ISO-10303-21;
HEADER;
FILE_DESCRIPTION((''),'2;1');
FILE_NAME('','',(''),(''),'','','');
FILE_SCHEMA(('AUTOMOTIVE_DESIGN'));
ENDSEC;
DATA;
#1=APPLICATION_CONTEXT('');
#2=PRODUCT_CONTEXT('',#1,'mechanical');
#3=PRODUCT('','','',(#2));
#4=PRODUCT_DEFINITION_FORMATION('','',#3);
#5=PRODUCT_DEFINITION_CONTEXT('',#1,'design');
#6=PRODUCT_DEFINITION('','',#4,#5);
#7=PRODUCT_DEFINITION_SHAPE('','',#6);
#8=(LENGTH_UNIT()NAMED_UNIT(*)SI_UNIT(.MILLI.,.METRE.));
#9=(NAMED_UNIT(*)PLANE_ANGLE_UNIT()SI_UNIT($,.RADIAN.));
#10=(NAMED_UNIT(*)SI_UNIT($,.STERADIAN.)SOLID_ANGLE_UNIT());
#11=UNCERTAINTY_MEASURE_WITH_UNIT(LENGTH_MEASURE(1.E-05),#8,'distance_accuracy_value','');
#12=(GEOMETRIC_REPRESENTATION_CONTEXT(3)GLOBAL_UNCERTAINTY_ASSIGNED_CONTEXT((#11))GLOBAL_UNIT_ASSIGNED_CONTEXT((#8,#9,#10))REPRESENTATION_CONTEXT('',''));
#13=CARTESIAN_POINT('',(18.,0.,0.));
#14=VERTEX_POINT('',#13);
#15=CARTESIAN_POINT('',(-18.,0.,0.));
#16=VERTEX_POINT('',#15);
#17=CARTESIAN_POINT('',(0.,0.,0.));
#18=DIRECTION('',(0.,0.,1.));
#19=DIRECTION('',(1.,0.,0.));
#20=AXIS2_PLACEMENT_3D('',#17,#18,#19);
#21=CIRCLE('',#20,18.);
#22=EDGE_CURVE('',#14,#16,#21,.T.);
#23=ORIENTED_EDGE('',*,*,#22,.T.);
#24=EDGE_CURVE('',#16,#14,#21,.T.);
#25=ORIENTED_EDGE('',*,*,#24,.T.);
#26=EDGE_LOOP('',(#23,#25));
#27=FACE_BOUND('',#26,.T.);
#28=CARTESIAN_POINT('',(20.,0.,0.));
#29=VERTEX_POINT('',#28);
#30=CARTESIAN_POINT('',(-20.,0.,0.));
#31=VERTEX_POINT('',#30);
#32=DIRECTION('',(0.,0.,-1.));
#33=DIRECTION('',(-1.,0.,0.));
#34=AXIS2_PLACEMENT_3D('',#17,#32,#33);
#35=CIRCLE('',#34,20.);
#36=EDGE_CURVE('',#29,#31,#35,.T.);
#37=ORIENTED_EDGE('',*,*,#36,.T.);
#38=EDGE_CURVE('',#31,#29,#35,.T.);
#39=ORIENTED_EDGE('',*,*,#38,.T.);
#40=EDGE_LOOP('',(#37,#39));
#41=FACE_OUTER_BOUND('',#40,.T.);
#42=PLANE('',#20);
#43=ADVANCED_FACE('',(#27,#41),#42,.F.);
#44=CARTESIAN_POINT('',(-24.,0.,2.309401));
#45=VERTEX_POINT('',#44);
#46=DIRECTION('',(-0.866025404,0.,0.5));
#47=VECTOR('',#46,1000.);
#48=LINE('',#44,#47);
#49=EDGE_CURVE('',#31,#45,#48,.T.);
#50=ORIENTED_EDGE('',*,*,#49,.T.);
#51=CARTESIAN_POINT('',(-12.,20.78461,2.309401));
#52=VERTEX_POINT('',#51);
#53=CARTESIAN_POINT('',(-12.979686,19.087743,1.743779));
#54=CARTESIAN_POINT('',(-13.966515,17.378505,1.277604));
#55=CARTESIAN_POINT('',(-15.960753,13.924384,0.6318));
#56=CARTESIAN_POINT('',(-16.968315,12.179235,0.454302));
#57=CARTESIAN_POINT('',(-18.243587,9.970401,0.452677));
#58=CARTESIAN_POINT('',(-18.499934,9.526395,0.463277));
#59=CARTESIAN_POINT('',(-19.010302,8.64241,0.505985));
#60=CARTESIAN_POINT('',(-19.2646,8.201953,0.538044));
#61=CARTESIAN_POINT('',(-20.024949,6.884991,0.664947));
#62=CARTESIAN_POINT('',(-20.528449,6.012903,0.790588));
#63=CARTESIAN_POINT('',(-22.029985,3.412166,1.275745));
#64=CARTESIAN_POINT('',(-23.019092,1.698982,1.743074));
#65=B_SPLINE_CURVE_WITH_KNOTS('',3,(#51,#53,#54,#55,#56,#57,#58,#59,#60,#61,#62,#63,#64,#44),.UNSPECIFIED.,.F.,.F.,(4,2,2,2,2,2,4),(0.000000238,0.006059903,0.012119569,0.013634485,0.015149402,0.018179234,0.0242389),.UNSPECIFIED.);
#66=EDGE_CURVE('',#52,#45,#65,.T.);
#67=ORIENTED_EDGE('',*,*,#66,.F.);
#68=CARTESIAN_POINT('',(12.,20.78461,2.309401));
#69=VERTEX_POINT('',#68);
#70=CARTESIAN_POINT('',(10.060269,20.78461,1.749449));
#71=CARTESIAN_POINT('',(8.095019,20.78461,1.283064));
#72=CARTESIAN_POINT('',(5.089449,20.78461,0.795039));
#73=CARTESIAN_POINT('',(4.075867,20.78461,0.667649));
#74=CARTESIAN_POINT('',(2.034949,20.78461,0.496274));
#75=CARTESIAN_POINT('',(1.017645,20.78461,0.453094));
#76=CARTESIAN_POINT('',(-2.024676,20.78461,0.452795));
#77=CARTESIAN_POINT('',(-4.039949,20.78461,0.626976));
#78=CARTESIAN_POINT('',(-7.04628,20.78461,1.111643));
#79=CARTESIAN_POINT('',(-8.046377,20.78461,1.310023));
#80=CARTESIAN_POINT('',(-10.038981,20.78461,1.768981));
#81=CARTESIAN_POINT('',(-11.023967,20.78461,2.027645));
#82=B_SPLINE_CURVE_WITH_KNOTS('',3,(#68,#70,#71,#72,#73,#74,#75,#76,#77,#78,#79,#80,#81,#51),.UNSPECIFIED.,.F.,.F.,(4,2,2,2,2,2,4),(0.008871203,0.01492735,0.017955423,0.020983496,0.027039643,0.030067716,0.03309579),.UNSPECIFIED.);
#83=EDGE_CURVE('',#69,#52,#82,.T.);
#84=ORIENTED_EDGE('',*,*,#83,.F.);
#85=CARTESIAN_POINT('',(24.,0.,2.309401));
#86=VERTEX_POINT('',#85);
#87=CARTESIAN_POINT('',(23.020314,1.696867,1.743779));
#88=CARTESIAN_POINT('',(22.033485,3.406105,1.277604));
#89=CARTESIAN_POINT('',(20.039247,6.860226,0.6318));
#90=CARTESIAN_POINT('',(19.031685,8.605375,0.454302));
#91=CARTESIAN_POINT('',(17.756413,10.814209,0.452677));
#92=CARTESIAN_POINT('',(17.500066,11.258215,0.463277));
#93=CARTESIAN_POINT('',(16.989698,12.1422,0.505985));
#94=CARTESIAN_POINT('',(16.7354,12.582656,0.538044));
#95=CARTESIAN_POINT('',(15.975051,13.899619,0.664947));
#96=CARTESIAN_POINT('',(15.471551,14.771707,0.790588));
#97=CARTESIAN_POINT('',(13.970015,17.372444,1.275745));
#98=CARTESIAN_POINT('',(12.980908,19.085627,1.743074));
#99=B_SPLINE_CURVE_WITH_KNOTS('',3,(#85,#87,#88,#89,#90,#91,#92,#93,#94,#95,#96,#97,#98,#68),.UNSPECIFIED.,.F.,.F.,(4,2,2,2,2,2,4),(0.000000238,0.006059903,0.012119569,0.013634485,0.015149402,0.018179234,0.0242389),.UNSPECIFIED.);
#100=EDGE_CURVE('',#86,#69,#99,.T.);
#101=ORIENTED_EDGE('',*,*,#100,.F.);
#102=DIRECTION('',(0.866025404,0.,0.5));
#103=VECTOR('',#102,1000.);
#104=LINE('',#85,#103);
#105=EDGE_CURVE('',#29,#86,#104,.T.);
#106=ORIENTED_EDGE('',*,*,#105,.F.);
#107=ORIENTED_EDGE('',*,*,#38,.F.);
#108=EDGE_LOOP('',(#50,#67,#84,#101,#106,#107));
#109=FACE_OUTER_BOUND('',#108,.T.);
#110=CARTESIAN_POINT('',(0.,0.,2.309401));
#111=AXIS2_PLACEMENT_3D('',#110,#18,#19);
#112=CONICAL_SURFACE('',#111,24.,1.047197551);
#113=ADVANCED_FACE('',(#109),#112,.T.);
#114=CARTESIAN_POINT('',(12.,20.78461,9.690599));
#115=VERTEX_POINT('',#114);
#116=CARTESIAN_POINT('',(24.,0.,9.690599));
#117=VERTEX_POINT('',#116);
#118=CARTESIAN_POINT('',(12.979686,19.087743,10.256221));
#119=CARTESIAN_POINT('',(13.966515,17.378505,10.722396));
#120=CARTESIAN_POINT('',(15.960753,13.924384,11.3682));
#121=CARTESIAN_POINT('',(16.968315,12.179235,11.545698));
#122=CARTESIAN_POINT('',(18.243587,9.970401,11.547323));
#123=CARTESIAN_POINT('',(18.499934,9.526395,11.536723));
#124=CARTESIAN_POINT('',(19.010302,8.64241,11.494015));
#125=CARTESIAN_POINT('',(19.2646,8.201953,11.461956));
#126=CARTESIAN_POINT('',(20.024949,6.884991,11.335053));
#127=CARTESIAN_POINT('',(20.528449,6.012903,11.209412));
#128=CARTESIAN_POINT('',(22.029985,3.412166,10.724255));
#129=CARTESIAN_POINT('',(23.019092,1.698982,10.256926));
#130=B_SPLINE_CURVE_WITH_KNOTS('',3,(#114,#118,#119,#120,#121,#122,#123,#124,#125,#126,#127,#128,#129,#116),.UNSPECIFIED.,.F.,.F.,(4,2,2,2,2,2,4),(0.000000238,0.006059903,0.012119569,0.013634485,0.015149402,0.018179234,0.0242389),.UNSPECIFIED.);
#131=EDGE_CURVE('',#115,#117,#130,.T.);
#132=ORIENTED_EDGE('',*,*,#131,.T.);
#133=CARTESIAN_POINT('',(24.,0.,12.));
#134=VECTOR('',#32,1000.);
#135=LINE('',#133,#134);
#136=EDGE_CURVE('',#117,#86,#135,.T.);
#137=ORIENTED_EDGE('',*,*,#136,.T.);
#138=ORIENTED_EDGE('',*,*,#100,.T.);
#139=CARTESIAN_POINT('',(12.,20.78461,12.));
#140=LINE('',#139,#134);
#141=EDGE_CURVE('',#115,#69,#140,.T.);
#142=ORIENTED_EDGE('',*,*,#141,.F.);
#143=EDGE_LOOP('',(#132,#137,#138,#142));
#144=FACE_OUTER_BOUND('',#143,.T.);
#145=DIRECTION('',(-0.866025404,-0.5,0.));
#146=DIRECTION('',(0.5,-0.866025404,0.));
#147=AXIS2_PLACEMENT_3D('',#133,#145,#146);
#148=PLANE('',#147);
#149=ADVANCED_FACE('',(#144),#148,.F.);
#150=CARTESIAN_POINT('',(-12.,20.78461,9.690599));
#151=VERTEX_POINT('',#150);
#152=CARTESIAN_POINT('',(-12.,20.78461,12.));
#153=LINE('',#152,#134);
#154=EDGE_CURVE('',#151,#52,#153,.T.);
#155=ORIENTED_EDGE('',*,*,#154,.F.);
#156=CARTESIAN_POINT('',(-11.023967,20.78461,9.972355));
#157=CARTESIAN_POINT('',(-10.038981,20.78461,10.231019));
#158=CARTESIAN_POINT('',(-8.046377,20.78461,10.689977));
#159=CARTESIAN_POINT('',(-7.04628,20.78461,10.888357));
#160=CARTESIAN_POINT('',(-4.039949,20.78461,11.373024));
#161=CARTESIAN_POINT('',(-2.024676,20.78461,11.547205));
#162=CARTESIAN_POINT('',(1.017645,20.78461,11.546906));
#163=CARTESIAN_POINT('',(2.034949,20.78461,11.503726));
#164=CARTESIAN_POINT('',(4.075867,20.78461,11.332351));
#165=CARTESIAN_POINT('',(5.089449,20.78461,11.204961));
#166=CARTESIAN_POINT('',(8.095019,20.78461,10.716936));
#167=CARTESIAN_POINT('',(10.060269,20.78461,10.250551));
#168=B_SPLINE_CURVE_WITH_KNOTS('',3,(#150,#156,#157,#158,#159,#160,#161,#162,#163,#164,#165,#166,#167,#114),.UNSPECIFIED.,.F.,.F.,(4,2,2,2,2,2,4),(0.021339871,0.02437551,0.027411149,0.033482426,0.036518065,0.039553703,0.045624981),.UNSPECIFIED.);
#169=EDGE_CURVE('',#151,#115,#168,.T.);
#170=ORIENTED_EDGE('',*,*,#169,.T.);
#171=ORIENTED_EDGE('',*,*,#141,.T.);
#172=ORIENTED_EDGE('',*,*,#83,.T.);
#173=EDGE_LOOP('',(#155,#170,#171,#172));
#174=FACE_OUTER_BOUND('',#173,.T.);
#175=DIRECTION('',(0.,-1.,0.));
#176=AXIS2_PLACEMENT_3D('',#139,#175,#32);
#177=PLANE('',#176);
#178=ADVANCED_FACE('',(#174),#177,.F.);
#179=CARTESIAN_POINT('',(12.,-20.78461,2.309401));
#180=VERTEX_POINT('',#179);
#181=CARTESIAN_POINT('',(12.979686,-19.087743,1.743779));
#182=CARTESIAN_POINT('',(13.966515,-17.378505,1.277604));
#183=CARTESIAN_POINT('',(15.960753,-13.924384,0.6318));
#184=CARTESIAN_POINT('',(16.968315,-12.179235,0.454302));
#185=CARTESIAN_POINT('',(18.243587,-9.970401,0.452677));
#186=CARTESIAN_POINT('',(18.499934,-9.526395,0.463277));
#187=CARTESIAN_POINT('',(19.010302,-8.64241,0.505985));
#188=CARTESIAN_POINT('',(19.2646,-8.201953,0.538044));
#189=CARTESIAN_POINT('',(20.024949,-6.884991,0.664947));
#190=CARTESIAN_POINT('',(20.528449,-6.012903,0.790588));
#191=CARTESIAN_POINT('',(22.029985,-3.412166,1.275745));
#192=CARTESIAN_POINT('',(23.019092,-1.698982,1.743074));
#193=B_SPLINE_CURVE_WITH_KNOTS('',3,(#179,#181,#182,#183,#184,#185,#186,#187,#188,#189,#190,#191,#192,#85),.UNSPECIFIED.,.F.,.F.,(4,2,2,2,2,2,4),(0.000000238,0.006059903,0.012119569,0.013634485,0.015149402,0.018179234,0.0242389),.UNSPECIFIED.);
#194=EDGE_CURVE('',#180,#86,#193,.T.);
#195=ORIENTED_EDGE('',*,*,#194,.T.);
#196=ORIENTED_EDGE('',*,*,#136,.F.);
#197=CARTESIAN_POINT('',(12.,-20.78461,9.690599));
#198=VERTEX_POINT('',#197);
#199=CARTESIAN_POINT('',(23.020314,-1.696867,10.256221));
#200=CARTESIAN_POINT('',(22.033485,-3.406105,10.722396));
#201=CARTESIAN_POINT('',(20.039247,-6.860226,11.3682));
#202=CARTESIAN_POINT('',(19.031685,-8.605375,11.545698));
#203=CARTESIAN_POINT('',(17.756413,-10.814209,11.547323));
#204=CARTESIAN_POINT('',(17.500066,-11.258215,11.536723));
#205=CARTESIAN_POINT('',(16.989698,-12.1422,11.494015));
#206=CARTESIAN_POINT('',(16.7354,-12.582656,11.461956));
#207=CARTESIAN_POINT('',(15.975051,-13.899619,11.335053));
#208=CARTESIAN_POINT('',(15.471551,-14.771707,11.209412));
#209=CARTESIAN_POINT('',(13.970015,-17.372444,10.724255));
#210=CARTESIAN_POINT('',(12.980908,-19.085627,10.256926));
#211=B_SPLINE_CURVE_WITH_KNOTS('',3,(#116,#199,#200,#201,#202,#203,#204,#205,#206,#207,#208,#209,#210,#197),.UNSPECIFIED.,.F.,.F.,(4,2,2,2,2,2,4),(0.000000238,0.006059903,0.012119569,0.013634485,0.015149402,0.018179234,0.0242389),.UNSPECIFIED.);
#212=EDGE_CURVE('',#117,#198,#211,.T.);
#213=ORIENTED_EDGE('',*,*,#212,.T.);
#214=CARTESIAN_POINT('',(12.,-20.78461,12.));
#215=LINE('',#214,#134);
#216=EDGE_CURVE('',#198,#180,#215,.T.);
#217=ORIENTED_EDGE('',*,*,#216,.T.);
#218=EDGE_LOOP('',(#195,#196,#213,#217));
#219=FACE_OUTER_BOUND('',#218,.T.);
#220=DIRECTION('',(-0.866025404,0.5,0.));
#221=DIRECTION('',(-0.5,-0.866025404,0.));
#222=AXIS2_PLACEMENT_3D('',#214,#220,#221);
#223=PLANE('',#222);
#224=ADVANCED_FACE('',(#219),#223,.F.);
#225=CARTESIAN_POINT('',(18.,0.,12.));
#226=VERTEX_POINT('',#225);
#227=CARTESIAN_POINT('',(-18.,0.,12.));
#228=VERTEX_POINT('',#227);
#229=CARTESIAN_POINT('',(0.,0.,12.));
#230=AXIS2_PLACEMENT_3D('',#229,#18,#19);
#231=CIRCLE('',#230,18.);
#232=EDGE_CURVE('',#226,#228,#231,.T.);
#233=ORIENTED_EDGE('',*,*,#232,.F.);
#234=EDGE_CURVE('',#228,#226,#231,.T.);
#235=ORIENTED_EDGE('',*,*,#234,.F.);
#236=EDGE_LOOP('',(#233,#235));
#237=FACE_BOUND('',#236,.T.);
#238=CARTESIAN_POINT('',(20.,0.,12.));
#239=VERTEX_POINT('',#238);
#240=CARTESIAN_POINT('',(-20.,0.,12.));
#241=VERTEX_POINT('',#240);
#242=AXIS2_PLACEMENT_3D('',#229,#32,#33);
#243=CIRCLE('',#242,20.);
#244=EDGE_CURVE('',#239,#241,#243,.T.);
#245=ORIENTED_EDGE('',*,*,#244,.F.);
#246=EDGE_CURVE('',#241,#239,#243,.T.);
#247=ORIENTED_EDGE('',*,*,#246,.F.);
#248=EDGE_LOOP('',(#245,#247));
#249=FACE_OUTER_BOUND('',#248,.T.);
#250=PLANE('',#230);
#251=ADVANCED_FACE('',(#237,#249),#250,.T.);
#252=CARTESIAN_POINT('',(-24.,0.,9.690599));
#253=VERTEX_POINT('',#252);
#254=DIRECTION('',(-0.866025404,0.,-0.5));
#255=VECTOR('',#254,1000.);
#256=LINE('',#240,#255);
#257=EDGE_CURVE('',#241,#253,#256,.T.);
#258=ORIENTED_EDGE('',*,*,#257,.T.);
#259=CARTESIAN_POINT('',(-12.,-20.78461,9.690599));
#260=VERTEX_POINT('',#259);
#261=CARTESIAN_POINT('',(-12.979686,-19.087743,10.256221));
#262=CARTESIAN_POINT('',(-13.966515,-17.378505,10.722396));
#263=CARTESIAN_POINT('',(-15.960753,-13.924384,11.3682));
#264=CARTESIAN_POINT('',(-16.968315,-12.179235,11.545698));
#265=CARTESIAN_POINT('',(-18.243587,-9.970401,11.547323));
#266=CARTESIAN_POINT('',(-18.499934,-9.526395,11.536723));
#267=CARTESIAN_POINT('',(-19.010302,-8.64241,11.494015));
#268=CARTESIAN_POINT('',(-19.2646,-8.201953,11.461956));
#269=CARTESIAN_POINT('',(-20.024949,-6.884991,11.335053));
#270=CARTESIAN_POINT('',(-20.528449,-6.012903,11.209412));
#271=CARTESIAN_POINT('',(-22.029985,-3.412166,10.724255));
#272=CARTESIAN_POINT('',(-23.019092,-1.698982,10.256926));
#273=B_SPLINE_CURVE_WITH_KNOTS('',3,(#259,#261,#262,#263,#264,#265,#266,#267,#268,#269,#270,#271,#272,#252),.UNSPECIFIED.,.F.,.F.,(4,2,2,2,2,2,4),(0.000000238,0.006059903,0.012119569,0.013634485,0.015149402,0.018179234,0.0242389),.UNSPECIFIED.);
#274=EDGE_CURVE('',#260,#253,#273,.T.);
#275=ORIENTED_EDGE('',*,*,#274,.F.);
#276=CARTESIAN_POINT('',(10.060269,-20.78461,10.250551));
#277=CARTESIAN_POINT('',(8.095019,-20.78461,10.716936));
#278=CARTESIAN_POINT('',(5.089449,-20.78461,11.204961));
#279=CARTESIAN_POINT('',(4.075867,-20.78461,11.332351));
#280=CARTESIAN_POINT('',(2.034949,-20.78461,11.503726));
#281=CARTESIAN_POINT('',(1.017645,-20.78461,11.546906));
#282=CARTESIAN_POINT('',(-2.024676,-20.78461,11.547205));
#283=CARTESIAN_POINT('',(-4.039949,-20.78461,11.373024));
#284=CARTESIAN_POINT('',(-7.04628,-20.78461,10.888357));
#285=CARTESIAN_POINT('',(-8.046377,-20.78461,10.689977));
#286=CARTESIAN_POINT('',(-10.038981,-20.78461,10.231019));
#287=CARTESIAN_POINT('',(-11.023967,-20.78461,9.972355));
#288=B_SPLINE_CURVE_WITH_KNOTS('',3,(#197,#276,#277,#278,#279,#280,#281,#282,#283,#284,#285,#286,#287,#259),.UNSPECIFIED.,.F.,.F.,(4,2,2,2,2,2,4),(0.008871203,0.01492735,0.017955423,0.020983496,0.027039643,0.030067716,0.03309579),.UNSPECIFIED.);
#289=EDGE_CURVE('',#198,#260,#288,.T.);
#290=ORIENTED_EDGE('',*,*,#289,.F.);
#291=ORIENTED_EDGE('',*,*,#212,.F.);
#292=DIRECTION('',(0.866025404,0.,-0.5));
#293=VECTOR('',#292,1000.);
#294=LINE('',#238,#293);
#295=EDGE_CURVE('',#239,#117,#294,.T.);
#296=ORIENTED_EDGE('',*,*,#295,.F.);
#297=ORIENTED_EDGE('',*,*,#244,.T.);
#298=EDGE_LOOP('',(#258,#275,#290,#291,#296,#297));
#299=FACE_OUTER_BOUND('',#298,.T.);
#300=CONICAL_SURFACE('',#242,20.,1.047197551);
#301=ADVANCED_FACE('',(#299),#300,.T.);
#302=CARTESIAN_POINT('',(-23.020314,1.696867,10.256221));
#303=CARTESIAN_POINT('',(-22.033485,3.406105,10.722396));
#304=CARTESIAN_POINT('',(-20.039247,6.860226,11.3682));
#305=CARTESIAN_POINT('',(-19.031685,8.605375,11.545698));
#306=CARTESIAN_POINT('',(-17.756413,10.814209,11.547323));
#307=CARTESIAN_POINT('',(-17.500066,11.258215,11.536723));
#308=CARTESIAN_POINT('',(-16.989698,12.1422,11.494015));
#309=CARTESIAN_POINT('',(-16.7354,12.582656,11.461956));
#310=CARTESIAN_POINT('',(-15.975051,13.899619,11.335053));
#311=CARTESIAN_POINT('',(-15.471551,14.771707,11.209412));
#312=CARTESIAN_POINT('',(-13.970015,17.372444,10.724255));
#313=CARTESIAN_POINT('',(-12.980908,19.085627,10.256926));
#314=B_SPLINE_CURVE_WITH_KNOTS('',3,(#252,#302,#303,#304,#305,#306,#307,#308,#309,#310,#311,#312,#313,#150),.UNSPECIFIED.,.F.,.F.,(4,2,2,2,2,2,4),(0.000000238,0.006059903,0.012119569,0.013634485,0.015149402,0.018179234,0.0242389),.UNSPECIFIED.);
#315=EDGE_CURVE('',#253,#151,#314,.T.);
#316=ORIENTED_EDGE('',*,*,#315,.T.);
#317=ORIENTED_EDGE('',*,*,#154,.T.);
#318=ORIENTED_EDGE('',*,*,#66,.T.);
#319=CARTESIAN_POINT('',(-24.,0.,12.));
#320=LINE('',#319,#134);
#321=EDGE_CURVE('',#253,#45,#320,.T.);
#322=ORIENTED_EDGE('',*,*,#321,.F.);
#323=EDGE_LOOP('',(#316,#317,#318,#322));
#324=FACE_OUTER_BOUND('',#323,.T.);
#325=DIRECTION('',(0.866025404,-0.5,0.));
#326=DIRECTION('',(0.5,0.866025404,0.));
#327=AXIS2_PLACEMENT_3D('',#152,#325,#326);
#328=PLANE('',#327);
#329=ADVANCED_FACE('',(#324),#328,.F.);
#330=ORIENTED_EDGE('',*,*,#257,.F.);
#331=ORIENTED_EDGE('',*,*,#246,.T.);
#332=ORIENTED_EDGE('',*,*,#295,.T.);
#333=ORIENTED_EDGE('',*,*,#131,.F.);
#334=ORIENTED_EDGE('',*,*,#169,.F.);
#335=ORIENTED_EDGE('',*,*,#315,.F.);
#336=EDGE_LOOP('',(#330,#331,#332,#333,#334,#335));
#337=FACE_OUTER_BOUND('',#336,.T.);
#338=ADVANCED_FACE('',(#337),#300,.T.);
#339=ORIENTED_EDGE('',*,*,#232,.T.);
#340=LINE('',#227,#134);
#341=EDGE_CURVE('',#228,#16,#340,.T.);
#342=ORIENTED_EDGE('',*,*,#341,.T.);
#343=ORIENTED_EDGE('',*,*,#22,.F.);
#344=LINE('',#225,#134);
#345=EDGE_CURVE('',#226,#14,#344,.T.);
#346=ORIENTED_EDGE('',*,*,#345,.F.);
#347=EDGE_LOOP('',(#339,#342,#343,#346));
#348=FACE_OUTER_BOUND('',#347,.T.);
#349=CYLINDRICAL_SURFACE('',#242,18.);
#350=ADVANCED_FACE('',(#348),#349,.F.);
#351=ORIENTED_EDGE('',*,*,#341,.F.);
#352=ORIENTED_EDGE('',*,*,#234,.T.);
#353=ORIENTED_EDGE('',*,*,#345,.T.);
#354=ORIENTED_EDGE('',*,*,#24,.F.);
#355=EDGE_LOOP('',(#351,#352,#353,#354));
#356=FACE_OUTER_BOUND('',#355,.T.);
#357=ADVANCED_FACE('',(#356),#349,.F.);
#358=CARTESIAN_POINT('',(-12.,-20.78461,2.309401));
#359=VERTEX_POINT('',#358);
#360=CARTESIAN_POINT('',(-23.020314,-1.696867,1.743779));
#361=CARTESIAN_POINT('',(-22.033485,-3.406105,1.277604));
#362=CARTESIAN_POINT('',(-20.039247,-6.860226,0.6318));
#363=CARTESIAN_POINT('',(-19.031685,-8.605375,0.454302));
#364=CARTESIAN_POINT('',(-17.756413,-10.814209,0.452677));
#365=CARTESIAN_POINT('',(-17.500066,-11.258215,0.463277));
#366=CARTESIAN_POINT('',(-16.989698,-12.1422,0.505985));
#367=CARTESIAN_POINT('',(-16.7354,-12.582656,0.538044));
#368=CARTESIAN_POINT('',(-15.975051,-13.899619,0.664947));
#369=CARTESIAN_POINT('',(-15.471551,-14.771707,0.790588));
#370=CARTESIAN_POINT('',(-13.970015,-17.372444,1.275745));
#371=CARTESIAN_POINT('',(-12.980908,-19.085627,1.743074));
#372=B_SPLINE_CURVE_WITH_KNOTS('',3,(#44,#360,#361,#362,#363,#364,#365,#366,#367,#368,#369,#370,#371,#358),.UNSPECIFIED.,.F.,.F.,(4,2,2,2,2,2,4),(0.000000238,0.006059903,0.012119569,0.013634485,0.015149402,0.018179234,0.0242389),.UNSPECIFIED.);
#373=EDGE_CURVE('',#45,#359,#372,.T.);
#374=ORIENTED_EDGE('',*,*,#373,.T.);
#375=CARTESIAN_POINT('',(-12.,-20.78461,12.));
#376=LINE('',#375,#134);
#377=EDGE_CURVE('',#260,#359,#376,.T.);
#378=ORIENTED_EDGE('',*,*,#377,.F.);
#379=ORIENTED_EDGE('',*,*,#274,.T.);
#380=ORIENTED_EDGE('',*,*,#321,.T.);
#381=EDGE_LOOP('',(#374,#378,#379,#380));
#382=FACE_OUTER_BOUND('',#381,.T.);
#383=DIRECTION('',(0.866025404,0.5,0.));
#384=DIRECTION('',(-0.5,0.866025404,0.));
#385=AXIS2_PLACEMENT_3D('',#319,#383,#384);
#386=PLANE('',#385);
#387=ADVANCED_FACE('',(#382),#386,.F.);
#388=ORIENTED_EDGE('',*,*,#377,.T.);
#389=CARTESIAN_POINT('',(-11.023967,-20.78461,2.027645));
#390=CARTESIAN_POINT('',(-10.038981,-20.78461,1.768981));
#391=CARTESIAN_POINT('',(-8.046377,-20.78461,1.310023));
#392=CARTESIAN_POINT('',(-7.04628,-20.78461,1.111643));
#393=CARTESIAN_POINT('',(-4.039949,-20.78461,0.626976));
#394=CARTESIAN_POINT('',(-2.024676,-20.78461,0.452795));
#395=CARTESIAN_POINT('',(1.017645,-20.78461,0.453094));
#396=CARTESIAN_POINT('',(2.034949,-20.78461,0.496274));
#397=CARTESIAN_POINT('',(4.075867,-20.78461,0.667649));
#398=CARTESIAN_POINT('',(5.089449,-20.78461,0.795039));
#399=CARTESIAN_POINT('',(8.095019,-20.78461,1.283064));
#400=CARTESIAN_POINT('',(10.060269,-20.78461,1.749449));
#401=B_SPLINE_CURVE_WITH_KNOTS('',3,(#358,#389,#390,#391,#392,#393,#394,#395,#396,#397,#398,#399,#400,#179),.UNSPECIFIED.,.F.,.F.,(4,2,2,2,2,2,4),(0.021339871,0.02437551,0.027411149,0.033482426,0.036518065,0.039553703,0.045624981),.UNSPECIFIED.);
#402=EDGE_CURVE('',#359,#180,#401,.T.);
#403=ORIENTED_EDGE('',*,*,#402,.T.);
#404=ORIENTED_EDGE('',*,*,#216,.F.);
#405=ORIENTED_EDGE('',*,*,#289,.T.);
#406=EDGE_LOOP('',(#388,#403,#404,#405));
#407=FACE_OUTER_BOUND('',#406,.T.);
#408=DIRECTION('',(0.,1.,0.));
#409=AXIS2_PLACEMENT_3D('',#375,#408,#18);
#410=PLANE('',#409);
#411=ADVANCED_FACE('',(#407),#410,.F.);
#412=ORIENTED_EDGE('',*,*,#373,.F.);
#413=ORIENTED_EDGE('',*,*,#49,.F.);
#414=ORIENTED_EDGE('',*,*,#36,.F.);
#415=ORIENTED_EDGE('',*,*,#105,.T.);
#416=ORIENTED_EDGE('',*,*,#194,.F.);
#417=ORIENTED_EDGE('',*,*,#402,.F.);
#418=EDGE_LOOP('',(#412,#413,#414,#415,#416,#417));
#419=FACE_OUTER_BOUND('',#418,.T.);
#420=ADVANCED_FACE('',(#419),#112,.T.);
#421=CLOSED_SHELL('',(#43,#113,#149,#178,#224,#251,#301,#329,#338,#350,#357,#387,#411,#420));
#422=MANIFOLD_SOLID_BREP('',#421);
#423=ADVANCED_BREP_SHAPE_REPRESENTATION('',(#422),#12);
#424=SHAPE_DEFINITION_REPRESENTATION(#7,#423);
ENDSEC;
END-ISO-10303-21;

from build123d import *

# Parameters (mm, degrees)
SKETCH_1_R      = 18
EXTRUDE_1_DEPTH = 12


with BuildPart() as part:
    # 草图1 → 凸台-拉伸1 (new body)
    with BuildSketch(Plane.XY):
        Polygon((24, 0), (12, 20.784609691), (-12, 20.784609691), (-24, 0), (-12, -20.784609691), (12, -20.784609691), align=None)
        Circle(SKETCH_1_R, mode=Mode.SUBTRACT)
    extrude(amount=EXTRUDE_1_DEPTH)

    # 草图2 → 切除-旋转1 (revolve, cut)
    with BuildSketch(Plane(origin=(0, 0, 0), x_dir=(1, 0, 0), z_dir=(0, 1, 0))):
        Polygon((-24, 0), (-24, -2.309401077), (-20, 0), align=None)
        Polygon((-24, -12), (-24, -9.690598923), (-20, -12), align=None)
    revolve(axis=Axis((0, 0, -5.971832554), (0, 0, 1)), mode=Mode.SUBTRACT)


solid = part.part
